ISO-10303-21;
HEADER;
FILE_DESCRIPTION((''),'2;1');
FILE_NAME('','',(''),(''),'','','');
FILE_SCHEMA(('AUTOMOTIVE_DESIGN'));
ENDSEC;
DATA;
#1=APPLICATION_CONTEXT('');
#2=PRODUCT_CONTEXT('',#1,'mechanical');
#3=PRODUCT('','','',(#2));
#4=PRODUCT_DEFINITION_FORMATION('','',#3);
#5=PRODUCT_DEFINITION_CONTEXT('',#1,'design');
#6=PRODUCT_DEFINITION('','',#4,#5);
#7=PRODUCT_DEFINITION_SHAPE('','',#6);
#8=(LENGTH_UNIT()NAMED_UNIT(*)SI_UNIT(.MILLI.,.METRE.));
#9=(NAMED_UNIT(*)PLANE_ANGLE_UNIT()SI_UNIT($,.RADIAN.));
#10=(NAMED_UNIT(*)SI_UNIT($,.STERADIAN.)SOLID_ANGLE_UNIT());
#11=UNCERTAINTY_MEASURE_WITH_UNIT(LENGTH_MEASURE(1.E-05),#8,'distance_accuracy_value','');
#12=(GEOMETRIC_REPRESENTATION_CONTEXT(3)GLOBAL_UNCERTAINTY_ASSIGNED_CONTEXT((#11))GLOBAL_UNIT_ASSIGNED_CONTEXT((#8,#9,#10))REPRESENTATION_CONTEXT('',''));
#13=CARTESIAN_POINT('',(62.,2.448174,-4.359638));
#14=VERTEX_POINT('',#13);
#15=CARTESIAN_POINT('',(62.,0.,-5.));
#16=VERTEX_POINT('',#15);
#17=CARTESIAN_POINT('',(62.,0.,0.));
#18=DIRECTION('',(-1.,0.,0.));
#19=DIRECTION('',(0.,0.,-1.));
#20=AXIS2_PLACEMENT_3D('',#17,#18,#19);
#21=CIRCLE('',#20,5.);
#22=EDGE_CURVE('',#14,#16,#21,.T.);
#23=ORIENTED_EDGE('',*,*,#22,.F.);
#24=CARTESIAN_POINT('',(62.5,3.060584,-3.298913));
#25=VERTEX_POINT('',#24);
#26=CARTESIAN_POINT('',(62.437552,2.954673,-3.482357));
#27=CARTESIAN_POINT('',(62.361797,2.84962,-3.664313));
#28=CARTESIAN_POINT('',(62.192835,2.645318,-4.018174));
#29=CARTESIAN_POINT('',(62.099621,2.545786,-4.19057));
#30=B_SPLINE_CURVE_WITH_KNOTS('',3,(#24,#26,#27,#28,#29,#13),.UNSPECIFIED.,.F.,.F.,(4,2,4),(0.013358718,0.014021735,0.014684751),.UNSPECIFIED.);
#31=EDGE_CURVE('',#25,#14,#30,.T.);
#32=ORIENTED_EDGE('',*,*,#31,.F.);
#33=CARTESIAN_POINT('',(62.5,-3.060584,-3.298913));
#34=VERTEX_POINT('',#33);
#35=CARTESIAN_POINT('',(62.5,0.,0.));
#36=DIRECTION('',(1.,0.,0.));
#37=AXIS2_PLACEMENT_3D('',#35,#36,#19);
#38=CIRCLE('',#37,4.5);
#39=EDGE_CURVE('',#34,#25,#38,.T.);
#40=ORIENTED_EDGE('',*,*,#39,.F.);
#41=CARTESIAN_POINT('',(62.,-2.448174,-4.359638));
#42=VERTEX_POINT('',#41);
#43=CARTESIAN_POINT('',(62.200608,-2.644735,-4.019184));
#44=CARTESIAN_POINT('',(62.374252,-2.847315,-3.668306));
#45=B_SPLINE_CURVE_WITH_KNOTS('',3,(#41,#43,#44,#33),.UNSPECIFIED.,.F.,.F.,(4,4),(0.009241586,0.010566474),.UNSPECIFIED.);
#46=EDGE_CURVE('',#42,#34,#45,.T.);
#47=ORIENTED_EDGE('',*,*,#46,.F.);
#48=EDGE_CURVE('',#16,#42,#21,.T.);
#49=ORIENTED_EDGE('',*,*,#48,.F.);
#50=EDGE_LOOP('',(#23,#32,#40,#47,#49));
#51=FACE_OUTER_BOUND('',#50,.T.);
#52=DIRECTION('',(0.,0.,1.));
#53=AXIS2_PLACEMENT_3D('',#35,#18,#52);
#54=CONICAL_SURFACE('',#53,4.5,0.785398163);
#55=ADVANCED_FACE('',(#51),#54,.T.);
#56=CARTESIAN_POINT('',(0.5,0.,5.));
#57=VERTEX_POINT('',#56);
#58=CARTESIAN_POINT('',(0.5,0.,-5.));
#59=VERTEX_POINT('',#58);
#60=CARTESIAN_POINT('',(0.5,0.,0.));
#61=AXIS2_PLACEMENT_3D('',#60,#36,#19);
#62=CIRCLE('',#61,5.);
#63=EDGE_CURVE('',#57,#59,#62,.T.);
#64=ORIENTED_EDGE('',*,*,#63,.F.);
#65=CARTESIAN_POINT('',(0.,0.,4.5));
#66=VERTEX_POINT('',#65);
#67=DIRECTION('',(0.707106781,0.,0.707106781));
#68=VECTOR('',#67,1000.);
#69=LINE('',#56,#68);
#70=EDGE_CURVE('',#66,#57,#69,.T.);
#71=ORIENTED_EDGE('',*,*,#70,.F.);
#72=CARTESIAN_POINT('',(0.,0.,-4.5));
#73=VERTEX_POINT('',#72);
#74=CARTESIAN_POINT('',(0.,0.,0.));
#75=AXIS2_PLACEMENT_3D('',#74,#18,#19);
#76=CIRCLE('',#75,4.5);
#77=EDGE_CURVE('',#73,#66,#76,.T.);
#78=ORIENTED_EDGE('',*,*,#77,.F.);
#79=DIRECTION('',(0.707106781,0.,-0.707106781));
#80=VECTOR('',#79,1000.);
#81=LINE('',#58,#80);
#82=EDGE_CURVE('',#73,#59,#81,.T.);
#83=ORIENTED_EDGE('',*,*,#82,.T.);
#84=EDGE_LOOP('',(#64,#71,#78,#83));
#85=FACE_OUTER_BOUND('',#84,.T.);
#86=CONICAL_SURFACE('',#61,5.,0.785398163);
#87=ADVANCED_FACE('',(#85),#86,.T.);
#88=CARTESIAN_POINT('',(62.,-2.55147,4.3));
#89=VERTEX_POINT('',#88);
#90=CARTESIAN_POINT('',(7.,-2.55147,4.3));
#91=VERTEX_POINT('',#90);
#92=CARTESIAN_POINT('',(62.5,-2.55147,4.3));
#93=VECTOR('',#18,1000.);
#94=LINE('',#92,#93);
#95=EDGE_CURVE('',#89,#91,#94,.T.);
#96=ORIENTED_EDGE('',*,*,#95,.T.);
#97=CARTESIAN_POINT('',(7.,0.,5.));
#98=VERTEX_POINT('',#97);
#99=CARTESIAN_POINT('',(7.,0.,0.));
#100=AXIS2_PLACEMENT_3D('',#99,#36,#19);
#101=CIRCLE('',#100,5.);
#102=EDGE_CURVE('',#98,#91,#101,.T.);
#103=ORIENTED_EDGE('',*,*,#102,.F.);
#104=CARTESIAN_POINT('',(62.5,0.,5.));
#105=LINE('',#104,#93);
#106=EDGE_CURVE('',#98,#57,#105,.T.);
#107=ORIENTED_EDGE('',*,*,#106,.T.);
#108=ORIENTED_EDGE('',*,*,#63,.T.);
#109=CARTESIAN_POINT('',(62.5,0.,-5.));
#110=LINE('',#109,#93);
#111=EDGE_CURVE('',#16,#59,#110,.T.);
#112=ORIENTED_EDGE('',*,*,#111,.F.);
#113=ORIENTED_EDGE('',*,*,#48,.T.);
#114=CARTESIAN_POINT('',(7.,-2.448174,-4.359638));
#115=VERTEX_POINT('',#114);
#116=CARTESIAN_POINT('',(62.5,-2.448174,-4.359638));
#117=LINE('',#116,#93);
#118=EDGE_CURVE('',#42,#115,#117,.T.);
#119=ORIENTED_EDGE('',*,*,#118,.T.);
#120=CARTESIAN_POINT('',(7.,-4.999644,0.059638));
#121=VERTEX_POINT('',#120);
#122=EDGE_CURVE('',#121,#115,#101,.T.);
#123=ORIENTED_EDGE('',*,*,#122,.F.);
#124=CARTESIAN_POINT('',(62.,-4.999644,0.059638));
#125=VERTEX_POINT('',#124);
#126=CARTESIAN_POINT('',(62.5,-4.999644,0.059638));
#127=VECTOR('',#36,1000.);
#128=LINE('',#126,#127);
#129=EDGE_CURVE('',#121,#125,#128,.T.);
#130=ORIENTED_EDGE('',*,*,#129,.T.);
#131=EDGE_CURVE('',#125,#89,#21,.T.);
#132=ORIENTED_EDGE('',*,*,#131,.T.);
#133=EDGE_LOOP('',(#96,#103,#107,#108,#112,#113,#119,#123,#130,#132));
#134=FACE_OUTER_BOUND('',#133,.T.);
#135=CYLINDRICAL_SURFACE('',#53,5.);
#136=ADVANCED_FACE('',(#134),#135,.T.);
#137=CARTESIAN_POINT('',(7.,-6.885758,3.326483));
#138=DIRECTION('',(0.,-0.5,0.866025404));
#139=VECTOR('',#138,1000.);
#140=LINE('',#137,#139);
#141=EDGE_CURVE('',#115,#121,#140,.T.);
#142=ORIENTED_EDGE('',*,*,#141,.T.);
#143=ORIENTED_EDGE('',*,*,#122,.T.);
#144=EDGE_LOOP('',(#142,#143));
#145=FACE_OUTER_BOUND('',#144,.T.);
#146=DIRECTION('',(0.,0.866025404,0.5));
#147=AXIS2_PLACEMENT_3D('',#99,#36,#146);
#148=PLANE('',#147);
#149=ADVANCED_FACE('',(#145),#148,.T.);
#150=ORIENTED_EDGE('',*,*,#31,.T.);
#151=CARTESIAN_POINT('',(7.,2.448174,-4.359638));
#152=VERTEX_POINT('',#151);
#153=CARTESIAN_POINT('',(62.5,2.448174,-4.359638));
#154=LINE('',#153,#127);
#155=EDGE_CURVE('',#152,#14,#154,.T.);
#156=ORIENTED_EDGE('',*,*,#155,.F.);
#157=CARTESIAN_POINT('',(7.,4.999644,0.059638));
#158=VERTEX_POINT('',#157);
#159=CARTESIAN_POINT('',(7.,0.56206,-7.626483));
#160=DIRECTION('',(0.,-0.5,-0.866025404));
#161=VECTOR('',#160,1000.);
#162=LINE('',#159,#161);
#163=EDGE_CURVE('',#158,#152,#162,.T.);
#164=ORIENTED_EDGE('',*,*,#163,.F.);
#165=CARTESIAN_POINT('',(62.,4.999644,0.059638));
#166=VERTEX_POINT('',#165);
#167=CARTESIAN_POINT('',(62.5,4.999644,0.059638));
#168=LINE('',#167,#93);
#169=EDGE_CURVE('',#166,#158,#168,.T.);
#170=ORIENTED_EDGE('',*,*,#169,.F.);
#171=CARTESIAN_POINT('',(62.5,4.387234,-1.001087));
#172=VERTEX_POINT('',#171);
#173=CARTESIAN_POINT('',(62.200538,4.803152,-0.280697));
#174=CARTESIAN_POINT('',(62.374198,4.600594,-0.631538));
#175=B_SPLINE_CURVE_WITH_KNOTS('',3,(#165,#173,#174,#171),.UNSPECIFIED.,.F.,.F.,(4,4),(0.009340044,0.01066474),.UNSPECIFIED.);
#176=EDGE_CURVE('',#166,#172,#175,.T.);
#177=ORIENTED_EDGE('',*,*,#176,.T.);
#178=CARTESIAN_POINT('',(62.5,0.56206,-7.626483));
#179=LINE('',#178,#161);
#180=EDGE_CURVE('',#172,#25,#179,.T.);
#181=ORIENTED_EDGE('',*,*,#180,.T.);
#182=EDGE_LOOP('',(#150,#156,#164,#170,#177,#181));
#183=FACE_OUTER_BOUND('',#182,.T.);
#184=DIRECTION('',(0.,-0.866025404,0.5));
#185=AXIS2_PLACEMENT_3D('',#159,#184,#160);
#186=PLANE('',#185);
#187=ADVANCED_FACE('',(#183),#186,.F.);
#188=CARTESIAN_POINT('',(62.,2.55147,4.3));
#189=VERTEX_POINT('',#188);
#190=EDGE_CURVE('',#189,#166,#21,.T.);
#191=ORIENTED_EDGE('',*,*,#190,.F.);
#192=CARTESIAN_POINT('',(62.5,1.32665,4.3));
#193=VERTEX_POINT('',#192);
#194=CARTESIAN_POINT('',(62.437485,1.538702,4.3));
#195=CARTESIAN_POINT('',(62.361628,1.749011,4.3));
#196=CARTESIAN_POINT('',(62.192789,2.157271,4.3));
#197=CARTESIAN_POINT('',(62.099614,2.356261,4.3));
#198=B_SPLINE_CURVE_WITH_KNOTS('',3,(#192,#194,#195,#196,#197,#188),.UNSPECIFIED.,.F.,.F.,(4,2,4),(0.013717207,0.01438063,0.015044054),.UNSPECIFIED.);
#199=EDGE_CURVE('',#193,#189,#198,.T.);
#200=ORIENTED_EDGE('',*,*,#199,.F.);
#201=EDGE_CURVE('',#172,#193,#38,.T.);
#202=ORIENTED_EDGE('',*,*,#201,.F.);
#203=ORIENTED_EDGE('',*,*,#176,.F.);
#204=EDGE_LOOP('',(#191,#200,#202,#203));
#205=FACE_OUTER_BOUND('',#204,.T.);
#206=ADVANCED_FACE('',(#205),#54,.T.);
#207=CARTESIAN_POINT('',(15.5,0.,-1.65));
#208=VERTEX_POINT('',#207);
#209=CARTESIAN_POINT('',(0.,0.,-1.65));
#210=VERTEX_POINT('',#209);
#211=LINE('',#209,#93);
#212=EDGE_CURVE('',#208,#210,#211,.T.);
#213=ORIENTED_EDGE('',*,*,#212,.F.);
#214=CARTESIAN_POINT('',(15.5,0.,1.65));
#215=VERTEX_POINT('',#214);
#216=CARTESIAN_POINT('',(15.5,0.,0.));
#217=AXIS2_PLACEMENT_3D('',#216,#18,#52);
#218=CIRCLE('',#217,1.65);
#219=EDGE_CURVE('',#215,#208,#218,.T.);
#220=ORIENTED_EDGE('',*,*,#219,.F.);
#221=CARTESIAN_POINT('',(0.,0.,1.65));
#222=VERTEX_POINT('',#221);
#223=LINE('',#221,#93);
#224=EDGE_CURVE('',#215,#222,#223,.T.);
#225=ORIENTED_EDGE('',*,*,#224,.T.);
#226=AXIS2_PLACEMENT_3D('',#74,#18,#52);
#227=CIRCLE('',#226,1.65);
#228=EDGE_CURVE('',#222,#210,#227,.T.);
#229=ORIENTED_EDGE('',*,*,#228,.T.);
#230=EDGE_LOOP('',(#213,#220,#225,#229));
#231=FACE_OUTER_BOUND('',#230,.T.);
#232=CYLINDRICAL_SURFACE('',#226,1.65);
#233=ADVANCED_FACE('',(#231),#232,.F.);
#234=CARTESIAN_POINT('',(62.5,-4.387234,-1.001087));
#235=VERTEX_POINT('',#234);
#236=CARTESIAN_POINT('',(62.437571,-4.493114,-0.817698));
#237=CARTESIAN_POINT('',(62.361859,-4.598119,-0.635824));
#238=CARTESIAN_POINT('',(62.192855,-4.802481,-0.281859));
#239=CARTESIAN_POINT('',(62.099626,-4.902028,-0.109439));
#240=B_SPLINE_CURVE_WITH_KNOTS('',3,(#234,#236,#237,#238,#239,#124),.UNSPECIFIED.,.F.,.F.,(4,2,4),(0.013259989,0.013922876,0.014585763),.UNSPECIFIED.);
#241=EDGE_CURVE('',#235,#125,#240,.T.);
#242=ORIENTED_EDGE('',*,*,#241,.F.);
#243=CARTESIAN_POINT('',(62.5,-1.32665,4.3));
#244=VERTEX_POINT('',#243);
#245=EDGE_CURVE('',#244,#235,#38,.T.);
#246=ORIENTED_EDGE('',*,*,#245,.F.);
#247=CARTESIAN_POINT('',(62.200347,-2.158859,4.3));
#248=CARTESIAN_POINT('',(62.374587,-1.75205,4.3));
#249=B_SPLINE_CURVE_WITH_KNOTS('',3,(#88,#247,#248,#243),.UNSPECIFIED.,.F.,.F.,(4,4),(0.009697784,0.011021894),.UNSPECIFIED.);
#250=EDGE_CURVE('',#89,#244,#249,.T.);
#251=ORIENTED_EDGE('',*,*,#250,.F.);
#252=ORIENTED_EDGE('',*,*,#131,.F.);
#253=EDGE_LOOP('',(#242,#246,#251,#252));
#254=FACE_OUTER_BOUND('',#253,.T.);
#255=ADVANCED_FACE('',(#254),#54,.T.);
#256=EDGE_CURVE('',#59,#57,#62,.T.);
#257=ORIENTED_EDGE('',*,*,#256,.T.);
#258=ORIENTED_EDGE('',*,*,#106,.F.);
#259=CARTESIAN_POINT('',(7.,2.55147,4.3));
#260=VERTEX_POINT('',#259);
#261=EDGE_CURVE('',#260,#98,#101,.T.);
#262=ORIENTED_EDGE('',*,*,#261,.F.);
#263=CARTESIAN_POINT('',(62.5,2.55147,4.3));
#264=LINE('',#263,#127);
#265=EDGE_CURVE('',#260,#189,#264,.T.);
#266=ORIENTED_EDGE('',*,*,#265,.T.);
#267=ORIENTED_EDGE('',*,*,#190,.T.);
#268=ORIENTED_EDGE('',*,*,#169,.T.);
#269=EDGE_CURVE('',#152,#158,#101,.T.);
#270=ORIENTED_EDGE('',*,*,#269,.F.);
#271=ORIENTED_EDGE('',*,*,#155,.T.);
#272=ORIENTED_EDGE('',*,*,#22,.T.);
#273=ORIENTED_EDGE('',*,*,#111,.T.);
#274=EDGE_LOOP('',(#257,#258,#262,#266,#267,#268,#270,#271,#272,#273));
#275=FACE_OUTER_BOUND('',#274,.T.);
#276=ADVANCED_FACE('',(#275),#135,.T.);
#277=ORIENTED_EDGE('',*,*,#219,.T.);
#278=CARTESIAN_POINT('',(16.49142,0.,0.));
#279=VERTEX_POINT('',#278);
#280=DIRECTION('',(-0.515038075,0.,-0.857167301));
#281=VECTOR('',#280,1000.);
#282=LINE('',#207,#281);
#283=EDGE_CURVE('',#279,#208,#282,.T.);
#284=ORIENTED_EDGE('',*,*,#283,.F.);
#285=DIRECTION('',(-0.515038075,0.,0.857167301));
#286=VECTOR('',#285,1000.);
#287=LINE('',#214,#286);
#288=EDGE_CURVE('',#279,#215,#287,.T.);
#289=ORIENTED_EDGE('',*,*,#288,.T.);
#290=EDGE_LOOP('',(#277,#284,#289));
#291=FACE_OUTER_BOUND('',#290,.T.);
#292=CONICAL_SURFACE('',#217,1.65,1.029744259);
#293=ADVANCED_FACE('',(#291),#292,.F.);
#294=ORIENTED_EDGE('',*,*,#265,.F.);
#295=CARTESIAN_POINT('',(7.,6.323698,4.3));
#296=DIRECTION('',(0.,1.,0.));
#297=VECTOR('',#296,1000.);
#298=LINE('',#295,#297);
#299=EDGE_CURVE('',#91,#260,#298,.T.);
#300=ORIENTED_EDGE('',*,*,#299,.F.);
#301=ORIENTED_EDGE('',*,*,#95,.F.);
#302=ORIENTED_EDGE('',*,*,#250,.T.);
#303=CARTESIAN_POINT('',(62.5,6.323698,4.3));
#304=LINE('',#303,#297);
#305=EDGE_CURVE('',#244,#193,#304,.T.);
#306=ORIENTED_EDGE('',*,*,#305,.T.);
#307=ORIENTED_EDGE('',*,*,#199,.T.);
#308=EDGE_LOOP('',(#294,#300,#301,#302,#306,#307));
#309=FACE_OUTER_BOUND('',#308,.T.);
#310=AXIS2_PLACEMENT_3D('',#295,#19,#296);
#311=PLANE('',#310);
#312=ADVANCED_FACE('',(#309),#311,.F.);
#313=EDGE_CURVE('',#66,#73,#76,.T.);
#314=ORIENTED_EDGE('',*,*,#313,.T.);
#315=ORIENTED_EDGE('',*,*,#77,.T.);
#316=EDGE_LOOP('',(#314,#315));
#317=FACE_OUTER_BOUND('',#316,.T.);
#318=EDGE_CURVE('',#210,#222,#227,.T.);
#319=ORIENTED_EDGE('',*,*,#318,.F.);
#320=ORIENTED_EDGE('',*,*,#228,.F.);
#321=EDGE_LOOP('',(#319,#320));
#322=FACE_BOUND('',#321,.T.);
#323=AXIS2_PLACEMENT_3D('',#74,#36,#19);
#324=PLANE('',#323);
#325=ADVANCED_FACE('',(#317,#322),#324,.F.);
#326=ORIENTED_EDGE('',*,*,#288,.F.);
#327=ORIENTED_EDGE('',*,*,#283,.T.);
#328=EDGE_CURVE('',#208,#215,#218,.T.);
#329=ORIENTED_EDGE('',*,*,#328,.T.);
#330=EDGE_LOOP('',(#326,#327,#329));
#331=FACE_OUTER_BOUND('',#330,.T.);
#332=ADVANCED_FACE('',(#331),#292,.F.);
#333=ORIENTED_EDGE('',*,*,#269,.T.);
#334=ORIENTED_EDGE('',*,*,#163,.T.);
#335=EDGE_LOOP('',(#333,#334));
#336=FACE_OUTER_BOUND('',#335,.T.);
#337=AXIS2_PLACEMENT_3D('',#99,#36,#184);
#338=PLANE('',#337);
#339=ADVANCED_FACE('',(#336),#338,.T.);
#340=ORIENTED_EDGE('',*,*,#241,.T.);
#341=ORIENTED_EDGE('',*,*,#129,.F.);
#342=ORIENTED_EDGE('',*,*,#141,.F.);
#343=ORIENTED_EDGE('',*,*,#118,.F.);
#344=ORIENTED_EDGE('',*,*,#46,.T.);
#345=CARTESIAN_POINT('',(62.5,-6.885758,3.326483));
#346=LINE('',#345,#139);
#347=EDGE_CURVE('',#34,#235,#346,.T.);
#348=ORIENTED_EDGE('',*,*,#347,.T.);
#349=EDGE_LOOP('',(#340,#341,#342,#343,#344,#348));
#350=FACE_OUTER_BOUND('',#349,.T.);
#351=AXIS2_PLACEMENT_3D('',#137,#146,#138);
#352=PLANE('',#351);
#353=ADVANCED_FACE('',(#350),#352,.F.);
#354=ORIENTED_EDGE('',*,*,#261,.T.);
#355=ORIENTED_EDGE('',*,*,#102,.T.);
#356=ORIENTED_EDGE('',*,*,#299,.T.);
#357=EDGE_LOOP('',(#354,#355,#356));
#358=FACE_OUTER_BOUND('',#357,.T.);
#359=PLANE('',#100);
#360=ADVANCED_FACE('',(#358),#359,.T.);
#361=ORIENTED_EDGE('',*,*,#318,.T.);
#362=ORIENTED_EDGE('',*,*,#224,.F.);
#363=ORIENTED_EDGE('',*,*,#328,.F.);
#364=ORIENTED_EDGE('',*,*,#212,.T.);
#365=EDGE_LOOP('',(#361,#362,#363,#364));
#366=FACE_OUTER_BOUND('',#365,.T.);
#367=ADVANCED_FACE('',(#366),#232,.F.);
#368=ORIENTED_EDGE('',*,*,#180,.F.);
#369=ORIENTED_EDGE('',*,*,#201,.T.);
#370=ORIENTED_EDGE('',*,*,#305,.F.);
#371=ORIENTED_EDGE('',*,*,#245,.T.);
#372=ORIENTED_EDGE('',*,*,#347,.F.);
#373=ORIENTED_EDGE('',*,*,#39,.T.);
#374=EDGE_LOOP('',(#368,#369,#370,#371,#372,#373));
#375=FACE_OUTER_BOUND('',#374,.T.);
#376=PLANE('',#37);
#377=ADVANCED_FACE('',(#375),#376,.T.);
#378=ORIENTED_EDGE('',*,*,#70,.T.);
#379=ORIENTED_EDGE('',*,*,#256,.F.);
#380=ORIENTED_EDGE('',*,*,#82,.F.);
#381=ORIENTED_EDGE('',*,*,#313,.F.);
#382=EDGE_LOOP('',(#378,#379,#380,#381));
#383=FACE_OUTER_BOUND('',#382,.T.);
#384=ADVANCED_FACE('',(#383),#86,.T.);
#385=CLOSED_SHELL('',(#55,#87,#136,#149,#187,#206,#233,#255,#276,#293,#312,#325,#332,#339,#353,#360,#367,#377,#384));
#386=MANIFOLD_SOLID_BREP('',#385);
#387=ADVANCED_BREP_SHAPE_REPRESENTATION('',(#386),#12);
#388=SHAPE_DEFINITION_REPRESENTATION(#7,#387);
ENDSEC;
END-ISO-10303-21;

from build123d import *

# Parameters (mm, degrees)
SKETCH_1_R               = 5
EXTRUDE_1_DEPTH          = 62.5
CHAMFER_1_SIZE           = 0.5
SKETCH_2_W               = 4.472118267
SKETCH_2_H               = 12.857340018
CUT_EXTRUDE_1_DEPTH      = 55.5
PATTERN_CIRCULAR_1_COUNT = 3
HOLE_WIZARD_M4_1_D       = 3.3
HOLE_WIZARD_M4_1_DEPTH   = 15.5
HOLE_WIZARD_M4_1_TIP     = 0.991420021


with BuildPart() as part:
    # 草图1 → 凸台-拉伸1 (new body)
    with BuildSketch(Plane(origin=(0, 0, 0), x_dir=(0, 0, -1), z_dir=(1, 0, 0))):
        Circle(SKETCH_1_R)
    extrude(amount=EXTRUDE_1_DEPTH)

    # 倒角1
    chamfer_1_edges = [part.edges().sort_by_distance(p)[0] for p in [
        (0, 0, 5),
        (62.5, 0, 5),
    ]]
    chamfer(chamfer_1_edges, length=CHAMFER_1_SIZE)

    # 草图2 → 切除-拉伸1 (cut)
    with BuildSketch(Plane(origin=(62.5, 0, 0), x_dir=(0, 0, -1), z_dir=(1, 0, 0))):
        with Locations((-6.536059134, -0.104972075)):
            Rectangle(SKETCH_2_W, SKETCH_2_H)
    cut_extrude_1 = extrude(amount=-CUT_EXTRUDE_1_DEPTH, mode=Mode.SUBTRACT)

    # 阵列(圆周)1: 切除-拉伸1 ×3 about axis
    pattern_circular_1_axis = Axis((0, 0, 0), (1, 0, 0))
    for i in range(1, PATTERN_CIRCULAR_1_COUNT):
        add(cut_extrude_1.rotate(pattern_circular_1_axis, i * 360 / PATTERN_CIRCULAR_1_COUNT), mode=Mode.SUBTRACT)

    # M4 螺纹孔1
    with Locations(Plane.ZY):
        with Locations((0, 0)):
            Hole(HOLE_WIZARD_M4_1_D / 2, depth=HOLE_WIZARD_M4_1_DEPTH)
            with Locations((0, 0, -(HOLE_WIZARD_M4_1_DEPTH + HOLE_WIZARD_M4_1_TIP / 2))):  # 118° drill point
                Cone(0, HOLE_WIZARD_M4_1_D / 2, HOLE_WIZARD_M4_1_TIP, mode=Mode.SUBTRACT)


solid = part.part
